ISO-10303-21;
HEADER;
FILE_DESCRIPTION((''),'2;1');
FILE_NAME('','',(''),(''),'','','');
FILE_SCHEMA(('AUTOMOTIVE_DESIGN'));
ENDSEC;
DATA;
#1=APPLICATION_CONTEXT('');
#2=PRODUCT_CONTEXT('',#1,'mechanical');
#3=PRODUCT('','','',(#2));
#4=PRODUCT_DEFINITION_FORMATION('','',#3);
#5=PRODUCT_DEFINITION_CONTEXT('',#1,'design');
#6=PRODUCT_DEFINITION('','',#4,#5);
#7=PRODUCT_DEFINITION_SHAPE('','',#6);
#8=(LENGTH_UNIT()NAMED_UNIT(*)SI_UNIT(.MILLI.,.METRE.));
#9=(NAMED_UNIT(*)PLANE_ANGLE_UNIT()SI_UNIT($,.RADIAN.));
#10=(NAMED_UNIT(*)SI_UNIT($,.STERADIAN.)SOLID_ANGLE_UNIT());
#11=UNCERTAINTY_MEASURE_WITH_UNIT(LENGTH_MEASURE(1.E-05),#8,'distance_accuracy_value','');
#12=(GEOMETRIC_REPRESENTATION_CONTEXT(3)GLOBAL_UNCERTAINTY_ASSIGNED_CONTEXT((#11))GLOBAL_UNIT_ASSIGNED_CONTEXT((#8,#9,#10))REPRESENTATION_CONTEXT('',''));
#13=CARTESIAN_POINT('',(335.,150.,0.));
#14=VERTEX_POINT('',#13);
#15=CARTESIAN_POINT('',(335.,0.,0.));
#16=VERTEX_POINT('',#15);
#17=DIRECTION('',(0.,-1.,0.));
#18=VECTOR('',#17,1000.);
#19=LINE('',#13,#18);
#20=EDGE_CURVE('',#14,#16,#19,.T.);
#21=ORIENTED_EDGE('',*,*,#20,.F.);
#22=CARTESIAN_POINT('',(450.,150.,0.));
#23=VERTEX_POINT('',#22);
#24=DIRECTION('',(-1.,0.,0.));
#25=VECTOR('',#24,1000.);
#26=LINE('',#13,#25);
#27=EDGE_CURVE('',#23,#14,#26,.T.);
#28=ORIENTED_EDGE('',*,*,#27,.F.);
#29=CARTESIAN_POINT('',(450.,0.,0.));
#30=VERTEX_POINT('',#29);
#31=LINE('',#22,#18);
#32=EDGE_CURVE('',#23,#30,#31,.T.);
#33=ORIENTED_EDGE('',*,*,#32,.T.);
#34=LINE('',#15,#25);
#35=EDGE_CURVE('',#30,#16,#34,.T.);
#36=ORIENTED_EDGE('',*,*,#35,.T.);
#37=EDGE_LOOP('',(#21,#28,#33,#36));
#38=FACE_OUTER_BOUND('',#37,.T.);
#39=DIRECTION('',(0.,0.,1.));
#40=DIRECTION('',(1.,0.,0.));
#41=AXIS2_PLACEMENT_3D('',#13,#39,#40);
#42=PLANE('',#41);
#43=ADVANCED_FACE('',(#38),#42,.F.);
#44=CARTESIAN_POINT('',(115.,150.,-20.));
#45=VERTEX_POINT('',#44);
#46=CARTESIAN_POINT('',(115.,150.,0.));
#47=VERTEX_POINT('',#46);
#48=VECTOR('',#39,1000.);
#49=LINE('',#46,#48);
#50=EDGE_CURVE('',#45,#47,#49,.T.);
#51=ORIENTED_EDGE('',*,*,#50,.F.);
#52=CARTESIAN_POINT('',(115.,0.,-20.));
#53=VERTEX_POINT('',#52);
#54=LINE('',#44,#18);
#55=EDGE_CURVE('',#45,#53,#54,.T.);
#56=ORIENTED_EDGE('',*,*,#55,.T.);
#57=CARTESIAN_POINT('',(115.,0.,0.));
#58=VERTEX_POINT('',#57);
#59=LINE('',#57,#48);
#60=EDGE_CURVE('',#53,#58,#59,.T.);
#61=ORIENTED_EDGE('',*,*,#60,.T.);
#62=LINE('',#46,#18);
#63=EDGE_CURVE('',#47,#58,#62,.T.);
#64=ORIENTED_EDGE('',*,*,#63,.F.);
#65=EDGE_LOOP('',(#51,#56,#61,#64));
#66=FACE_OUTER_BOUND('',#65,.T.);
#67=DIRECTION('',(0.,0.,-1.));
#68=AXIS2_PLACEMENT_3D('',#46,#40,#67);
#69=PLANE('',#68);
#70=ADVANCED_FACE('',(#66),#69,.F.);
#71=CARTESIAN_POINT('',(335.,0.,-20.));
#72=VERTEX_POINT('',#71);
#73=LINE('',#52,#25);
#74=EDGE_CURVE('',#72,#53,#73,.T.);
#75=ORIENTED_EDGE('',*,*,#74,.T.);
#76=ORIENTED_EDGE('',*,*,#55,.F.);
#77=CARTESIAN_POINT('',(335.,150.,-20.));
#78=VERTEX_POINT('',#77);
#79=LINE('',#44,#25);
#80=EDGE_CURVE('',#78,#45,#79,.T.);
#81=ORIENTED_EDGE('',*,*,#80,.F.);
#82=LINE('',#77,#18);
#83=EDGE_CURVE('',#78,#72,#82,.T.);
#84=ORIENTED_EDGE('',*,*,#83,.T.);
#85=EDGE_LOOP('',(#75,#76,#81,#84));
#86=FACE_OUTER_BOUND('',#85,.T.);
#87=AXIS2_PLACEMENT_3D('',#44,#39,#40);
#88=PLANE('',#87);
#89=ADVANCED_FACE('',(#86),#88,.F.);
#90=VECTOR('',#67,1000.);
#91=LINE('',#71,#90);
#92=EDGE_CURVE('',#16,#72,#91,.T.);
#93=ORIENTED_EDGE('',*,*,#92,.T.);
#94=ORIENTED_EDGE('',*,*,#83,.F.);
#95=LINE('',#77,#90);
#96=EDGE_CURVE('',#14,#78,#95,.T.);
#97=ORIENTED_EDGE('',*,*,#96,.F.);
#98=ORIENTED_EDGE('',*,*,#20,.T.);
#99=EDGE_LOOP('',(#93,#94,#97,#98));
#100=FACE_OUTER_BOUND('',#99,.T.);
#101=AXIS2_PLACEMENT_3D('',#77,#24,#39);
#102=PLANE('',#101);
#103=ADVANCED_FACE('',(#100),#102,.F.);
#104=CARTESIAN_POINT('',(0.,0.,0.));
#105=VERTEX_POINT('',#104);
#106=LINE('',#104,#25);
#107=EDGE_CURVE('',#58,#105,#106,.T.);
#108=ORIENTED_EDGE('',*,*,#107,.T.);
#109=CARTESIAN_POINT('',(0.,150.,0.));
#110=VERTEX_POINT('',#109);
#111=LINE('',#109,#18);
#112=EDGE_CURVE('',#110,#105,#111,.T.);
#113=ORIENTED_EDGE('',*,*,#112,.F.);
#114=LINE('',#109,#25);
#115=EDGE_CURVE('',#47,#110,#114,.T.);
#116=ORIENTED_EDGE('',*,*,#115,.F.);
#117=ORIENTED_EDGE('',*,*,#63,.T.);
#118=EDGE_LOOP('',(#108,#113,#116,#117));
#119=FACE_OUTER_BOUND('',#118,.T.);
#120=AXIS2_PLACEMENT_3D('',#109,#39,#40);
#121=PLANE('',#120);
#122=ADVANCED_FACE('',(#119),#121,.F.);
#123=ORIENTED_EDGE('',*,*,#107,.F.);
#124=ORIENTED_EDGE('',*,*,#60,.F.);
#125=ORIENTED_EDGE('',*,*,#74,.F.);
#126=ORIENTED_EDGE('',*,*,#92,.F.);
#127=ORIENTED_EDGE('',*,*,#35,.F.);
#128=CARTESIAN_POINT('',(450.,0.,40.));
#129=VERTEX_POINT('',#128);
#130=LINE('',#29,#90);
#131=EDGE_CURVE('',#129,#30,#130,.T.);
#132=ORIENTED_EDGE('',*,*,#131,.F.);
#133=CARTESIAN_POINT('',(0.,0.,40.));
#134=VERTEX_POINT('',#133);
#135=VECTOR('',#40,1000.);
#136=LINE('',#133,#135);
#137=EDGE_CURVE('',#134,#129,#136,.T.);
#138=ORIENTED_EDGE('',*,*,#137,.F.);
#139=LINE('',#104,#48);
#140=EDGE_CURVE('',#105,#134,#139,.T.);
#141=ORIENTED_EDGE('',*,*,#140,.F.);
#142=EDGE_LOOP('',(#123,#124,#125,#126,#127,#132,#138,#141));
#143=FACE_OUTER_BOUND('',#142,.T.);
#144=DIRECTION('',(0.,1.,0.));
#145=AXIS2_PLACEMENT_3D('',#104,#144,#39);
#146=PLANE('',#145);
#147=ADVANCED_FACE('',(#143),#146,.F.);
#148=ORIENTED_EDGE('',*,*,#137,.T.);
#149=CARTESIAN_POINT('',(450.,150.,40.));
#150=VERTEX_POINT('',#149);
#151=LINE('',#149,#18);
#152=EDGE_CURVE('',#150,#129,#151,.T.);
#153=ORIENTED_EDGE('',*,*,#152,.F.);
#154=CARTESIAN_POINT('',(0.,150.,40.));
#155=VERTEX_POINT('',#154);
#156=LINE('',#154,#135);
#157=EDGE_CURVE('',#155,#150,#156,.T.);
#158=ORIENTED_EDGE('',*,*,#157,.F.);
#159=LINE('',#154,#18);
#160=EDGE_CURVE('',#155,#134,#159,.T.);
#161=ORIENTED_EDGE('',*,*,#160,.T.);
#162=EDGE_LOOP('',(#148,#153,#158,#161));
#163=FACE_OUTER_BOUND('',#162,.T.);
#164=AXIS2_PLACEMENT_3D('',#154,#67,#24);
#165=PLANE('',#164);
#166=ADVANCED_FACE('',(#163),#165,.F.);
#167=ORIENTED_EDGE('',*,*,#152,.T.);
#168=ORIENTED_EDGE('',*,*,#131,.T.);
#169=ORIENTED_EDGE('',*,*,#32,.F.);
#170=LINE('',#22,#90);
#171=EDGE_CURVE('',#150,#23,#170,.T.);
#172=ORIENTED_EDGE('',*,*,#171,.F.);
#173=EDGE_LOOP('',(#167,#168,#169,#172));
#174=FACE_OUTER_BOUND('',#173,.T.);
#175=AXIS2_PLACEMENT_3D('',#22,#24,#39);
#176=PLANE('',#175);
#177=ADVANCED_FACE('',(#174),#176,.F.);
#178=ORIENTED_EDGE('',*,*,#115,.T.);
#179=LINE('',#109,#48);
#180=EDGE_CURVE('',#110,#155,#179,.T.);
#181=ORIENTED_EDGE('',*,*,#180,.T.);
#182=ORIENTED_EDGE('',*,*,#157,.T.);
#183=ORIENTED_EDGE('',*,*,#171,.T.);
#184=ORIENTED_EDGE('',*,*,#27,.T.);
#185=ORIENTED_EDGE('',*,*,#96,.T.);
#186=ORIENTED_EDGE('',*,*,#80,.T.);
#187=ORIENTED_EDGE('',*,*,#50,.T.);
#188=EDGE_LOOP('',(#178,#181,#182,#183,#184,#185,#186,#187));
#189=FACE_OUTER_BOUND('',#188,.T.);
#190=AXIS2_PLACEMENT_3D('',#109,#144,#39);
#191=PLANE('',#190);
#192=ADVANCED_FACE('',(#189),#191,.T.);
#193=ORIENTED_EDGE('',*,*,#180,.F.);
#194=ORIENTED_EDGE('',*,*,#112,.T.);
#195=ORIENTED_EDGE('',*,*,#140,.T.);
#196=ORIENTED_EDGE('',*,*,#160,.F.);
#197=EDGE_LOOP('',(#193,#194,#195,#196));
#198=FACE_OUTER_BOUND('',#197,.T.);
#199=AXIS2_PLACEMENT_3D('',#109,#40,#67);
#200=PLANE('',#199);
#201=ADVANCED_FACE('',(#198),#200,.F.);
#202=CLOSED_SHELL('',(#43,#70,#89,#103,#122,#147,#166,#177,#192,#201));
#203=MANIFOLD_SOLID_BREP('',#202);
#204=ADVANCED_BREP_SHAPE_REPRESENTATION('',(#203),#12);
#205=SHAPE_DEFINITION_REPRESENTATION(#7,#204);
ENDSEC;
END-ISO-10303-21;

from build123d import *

# Parameters (mm, degrees)
BOSS_EXTRUDE1_DEPTH = 150


with BuildPart() as part:
    # Sketch1 → Boss-Extrude1 (new body)
    with BuildSketch(Plane(origin=(0, 0, 0), x_dir=(1, 0, 0), z_dir=(0, 1, 0))):
        Polygon((115, 0), (115, 20), (335, 20), (335, 0), (450, 0), (450, -40), (0, -40), (0, 0), align=None)
    extrude(amount=BOSS_EXTRUDE1_DEPTH)


solid = part.part
